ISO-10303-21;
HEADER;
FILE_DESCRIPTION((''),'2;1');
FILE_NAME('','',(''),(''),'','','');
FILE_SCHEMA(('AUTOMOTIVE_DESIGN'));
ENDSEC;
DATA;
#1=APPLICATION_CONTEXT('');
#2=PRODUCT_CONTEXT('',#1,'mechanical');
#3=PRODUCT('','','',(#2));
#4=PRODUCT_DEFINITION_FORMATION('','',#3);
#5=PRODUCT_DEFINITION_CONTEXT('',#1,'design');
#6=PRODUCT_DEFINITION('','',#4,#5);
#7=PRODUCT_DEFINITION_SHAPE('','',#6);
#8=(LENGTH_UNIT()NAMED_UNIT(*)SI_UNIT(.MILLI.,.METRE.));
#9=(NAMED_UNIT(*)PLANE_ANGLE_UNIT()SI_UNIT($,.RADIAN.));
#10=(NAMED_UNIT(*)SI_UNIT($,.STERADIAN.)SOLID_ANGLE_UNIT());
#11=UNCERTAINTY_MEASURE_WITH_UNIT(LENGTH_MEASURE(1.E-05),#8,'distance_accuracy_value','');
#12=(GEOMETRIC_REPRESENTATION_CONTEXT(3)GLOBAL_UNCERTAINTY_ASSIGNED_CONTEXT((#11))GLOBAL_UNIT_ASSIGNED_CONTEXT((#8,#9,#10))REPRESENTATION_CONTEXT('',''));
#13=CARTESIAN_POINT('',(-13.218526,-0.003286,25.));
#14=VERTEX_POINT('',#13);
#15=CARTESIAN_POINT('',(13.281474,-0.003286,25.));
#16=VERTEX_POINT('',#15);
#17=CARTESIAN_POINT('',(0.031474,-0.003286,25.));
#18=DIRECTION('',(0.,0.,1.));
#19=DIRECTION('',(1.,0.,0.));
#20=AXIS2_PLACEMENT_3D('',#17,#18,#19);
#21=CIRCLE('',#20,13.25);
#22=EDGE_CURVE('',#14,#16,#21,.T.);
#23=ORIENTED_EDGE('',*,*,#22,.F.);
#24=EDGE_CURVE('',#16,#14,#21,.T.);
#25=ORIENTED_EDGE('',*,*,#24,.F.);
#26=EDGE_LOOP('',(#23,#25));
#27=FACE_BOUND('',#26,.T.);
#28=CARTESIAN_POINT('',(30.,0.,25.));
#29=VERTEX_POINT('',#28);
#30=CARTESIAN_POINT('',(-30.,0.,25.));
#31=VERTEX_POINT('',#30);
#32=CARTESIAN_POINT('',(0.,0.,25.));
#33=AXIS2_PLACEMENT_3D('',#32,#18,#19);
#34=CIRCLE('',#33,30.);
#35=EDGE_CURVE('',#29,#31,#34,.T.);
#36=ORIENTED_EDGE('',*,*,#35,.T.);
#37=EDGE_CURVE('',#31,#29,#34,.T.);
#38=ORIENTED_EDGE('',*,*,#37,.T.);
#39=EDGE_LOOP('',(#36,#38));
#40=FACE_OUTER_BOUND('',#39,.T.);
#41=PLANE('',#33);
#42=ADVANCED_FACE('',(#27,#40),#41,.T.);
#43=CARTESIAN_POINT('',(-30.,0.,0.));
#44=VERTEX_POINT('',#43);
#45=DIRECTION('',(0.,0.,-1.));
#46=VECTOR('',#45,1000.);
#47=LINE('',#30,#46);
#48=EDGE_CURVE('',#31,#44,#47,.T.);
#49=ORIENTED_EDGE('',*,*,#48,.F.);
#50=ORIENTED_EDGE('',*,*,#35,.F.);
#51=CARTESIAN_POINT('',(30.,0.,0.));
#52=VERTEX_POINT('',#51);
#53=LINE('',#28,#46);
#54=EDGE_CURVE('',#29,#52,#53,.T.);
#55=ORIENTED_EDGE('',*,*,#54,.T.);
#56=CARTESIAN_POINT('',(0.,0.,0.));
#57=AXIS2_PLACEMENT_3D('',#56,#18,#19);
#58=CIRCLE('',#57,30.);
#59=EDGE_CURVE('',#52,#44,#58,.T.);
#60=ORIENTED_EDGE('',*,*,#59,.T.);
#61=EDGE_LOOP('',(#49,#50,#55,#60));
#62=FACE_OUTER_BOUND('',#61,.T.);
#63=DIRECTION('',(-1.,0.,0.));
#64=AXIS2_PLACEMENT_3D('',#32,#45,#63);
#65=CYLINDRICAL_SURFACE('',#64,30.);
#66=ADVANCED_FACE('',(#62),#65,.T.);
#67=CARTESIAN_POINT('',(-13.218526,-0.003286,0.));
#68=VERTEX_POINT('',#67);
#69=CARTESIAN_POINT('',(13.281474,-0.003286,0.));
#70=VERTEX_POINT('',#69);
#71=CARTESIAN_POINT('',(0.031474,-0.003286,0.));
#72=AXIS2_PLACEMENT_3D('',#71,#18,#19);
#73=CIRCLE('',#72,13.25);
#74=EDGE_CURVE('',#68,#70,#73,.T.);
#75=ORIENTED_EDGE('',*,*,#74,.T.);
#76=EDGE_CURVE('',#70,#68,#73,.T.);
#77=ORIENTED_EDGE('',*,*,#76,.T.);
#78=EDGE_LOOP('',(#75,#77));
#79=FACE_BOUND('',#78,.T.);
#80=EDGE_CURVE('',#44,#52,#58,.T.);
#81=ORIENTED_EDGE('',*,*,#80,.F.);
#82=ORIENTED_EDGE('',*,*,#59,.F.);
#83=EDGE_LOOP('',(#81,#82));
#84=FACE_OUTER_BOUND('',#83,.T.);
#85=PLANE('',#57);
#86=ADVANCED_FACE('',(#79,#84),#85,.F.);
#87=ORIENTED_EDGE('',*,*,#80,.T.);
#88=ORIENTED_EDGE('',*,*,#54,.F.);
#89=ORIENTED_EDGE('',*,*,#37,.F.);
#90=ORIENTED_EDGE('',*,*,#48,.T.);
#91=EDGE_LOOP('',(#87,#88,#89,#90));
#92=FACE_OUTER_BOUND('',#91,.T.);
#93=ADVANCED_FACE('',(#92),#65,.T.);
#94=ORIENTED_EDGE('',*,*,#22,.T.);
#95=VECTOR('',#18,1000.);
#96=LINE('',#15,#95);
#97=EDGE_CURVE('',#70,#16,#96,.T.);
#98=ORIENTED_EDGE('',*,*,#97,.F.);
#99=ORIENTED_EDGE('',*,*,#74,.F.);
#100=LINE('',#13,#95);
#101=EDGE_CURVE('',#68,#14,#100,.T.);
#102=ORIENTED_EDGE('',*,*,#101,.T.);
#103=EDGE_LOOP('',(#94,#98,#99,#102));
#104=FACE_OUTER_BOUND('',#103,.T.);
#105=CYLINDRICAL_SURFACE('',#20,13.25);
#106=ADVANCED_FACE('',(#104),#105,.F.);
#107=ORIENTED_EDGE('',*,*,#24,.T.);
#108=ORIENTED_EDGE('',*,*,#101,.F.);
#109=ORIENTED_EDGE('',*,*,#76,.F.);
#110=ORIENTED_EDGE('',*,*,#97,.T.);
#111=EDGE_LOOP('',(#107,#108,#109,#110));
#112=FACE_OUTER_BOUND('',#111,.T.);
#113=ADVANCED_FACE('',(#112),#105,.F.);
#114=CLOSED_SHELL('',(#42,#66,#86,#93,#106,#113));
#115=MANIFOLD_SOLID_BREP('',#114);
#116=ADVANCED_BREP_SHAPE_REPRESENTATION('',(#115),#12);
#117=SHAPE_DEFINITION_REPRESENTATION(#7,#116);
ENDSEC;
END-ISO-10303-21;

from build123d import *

# Parameters (mm, degrees)
SKETCH1_R              = 30
BOSS_EXTRUDE1_DEPTH    = 25
M30_TAPPED_HOLE3_D     = 26.5
M30_TAPPED_HOLE3_DEPTH = 70.5
M30_TAPPED_HOLE3_TIP   = 7.961403202


with BuildPart() as part:
    # Sketch1 → Boss-Extrude1 (new body)
    with BuildSketch(Plane.XY):
        Circle(SKETCH1_R)
    extrude(amount=BOSS_EXTRUDE1_DEPTH)

    # M30 Tapped Hole3
    with Locations(Plane(origin=(0.031473792, -0.003286401, 25), x_dir=(1, 0, 0), z_dir=(0, 0, 1))):
        with Locations((0, 0)):
            Hole(M30_TAPPED_HOLE3_D / 2, depth=M30_TAPPED_HOLE3_DEPTH)
            with Locations((0, 0, -(M30_TAPPED_HOLE3_DEPTH + M30_TAPPED_HOLE3_TIP / 2))):  # 118° drill point
                Cone(0, M30_TAPPED_HOLE3_D / 2, M30_TAPPED_HOLE3_TIP, mode=Mode.SUBTRACT)


solid = part.part
